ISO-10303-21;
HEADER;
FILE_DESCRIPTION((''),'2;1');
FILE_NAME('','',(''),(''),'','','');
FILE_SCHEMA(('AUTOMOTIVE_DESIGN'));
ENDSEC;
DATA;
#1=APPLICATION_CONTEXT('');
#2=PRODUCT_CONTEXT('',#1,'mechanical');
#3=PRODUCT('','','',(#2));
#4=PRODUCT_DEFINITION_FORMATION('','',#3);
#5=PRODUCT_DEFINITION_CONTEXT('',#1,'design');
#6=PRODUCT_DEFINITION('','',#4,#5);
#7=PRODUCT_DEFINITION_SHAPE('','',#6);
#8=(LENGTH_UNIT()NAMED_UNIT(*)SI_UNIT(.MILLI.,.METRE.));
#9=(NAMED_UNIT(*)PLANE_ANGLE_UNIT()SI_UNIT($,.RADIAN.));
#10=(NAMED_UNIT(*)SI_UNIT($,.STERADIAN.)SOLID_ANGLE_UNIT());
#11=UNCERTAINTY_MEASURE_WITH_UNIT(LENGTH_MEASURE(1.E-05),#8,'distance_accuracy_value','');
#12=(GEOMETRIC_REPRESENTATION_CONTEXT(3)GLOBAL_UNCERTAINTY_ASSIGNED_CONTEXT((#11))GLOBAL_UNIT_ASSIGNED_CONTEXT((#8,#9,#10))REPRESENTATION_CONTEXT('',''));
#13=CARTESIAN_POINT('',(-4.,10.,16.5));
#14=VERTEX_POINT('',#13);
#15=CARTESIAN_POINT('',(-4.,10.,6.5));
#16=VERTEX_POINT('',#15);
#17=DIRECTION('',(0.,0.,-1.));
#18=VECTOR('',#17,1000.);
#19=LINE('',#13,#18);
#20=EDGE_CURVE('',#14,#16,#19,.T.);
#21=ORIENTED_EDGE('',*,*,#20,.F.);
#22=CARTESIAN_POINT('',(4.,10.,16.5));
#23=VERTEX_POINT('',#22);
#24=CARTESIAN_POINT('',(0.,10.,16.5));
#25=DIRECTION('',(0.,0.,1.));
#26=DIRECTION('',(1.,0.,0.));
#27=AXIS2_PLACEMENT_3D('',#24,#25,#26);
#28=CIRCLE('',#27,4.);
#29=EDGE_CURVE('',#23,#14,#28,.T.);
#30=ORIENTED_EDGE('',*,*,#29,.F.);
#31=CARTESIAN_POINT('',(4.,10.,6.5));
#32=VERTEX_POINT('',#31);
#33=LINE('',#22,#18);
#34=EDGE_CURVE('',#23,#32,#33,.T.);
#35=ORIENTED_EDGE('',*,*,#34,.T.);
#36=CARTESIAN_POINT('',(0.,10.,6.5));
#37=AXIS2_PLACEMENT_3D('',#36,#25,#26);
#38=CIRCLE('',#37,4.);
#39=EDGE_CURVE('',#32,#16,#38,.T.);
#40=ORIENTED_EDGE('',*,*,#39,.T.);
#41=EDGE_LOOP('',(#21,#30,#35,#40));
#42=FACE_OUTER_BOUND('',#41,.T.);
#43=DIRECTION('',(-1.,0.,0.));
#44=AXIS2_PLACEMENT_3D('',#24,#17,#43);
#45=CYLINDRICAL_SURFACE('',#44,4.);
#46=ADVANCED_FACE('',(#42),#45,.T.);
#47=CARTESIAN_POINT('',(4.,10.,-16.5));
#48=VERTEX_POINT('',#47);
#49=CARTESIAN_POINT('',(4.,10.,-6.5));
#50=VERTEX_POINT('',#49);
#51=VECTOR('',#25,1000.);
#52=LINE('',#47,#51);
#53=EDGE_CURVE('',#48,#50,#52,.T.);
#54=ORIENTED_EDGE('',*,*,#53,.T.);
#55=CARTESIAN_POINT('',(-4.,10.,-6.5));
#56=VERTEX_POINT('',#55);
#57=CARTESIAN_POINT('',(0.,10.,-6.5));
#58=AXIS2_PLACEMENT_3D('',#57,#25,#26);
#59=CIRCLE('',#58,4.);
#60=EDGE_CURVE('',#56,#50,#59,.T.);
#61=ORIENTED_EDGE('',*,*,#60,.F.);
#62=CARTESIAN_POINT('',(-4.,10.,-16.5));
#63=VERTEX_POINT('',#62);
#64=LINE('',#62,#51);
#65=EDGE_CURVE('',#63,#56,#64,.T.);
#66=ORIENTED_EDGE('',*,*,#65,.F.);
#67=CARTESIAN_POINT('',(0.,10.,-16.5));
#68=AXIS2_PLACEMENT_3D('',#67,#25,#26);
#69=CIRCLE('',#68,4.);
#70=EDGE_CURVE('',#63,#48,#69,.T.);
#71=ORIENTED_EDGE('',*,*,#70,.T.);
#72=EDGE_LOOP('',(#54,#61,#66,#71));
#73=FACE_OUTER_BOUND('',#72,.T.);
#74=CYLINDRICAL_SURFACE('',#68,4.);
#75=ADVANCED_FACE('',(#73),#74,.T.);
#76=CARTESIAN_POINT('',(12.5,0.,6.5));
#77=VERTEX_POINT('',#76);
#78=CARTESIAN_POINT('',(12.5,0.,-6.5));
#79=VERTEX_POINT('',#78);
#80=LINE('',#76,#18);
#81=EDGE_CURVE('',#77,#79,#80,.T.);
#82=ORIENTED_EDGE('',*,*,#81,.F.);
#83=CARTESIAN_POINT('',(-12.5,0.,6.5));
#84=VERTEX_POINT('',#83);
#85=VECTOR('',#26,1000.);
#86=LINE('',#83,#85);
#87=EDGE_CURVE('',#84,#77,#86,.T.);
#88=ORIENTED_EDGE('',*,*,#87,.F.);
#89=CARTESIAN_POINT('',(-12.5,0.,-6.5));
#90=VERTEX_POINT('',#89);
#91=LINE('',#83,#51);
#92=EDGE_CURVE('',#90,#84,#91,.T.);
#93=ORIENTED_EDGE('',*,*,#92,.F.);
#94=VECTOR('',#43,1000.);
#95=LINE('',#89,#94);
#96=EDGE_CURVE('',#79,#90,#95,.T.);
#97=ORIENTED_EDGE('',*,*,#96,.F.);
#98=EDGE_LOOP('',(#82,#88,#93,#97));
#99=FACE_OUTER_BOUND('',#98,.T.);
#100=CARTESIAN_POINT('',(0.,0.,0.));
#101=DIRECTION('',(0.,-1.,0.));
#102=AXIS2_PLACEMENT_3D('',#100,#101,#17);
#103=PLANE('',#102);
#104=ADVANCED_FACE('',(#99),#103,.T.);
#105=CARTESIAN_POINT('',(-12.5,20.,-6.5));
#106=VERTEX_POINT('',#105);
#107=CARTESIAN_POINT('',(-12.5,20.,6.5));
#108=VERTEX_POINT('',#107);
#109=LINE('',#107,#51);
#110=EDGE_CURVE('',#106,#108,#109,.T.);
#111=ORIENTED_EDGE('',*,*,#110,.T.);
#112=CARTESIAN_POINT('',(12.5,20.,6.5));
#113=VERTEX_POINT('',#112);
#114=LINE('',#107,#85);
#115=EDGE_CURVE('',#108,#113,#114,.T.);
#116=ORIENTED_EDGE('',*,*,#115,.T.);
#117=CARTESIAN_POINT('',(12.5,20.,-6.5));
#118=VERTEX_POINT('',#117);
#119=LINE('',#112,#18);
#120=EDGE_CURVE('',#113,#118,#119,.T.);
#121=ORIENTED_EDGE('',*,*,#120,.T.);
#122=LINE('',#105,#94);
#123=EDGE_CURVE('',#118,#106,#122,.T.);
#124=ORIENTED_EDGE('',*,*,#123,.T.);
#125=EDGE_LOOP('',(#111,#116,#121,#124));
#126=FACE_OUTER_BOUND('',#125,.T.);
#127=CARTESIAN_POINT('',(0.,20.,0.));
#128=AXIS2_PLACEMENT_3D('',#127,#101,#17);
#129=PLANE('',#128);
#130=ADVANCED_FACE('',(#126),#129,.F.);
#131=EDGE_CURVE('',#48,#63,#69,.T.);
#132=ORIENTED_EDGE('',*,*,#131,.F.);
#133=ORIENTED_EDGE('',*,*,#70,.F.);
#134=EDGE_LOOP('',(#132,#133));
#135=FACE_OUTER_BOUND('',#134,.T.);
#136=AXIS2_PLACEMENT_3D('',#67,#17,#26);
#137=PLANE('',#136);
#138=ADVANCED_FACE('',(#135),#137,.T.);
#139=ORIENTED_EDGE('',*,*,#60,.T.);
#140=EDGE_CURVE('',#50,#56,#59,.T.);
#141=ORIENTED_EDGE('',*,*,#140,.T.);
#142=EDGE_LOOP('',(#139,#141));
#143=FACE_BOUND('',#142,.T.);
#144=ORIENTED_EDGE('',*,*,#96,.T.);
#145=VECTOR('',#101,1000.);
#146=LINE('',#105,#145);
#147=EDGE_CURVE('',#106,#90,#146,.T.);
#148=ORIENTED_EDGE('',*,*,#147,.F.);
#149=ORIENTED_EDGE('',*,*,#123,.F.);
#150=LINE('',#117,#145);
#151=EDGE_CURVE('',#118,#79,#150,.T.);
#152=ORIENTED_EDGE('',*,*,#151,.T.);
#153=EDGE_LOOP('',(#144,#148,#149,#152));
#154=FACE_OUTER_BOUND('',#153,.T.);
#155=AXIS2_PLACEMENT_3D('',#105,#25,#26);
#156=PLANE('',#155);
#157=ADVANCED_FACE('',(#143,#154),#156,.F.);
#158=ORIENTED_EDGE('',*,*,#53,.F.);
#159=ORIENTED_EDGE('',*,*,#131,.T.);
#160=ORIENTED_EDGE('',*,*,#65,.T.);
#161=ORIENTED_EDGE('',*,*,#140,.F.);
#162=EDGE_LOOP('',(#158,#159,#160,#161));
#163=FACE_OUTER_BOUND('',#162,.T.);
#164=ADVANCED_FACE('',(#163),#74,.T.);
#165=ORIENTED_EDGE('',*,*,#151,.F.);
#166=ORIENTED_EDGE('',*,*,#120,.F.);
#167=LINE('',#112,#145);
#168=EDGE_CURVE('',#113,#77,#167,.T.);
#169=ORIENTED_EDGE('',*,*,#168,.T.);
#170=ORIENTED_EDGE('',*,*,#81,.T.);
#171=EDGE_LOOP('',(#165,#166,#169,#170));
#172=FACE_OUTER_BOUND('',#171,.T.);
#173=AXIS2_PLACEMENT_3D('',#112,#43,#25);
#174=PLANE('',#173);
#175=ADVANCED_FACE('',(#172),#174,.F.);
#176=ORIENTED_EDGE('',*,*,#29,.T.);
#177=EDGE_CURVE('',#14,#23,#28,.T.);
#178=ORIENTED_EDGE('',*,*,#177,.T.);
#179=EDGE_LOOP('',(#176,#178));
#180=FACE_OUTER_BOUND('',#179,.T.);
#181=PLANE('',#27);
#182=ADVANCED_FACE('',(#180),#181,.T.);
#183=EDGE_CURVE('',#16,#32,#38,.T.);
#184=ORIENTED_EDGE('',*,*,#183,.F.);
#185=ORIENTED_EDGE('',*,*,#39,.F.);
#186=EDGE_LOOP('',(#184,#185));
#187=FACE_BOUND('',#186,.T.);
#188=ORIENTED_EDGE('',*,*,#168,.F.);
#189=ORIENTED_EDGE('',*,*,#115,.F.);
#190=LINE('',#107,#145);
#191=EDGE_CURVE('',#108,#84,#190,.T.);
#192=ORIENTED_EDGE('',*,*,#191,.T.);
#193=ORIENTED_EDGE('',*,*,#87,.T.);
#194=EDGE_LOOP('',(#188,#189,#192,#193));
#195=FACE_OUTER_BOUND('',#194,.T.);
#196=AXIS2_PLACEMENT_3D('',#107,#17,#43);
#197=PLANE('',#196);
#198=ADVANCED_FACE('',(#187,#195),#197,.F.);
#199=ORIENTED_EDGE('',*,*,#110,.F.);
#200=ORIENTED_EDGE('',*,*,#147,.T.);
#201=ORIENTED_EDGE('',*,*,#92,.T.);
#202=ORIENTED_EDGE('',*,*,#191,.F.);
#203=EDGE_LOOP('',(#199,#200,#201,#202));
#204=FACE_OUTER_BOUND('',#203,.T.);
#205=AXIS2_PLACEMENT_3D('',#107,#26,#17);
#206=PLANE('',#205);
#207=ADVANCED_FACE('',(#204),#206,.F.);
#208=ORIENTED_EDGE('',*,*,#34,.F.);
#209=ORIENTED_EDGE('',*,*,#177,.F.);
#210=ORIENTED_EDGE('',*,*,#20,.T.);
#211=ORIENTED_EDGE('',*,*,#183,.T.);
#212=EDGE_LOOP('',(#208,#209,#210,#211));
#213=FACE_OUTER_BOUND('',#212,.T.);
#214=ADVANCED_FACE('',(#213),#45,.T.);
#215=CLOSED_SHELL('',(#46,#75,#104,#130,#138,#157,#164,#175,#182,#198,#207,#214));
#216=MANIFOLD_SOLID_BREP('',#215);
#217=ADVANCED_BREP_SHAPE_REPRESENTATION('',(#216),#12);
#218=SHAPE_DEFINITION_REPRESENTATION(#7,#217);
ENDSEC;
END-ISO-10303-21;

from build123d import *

# Parameters (mm, degrees)
SKETCH1_W           = 25
SKETCH1_H           = 13
BOSS_EXTRUDE1_DEPTH = 20
SKETCH2_R           = 4
BOSS_EXTRUDE2_DEPTH = 10


with BuildPart() as part:
    # Sketch1 → Boss-Extrude1 (new body)
    with BuildSketch(Plane(origin=(0, 0, 0), x_dir=(1, 0, 0), z_dir=(0, 1, 0))):
        Rectangle(SKETCH1_W, SKETCH1_H)
    extrude(amount=BOSS_EXTRUDE1_DEPTH)

    # Sketch2 → Boss-Extrude2 (add)
    with BuildSketch(Plane.XY.offset(6.5)):
        with Locations((0, 10)):
            Circle(SKETCH2_R)
    boss_extrude2 = extrude(amount=BOSS_EXTRUDE2_DEPTH)

    # Mirror1: Boss-Extrude2 across plane
    add(boss_extrude2.mirror(Plane.XY))


solid = part.part
